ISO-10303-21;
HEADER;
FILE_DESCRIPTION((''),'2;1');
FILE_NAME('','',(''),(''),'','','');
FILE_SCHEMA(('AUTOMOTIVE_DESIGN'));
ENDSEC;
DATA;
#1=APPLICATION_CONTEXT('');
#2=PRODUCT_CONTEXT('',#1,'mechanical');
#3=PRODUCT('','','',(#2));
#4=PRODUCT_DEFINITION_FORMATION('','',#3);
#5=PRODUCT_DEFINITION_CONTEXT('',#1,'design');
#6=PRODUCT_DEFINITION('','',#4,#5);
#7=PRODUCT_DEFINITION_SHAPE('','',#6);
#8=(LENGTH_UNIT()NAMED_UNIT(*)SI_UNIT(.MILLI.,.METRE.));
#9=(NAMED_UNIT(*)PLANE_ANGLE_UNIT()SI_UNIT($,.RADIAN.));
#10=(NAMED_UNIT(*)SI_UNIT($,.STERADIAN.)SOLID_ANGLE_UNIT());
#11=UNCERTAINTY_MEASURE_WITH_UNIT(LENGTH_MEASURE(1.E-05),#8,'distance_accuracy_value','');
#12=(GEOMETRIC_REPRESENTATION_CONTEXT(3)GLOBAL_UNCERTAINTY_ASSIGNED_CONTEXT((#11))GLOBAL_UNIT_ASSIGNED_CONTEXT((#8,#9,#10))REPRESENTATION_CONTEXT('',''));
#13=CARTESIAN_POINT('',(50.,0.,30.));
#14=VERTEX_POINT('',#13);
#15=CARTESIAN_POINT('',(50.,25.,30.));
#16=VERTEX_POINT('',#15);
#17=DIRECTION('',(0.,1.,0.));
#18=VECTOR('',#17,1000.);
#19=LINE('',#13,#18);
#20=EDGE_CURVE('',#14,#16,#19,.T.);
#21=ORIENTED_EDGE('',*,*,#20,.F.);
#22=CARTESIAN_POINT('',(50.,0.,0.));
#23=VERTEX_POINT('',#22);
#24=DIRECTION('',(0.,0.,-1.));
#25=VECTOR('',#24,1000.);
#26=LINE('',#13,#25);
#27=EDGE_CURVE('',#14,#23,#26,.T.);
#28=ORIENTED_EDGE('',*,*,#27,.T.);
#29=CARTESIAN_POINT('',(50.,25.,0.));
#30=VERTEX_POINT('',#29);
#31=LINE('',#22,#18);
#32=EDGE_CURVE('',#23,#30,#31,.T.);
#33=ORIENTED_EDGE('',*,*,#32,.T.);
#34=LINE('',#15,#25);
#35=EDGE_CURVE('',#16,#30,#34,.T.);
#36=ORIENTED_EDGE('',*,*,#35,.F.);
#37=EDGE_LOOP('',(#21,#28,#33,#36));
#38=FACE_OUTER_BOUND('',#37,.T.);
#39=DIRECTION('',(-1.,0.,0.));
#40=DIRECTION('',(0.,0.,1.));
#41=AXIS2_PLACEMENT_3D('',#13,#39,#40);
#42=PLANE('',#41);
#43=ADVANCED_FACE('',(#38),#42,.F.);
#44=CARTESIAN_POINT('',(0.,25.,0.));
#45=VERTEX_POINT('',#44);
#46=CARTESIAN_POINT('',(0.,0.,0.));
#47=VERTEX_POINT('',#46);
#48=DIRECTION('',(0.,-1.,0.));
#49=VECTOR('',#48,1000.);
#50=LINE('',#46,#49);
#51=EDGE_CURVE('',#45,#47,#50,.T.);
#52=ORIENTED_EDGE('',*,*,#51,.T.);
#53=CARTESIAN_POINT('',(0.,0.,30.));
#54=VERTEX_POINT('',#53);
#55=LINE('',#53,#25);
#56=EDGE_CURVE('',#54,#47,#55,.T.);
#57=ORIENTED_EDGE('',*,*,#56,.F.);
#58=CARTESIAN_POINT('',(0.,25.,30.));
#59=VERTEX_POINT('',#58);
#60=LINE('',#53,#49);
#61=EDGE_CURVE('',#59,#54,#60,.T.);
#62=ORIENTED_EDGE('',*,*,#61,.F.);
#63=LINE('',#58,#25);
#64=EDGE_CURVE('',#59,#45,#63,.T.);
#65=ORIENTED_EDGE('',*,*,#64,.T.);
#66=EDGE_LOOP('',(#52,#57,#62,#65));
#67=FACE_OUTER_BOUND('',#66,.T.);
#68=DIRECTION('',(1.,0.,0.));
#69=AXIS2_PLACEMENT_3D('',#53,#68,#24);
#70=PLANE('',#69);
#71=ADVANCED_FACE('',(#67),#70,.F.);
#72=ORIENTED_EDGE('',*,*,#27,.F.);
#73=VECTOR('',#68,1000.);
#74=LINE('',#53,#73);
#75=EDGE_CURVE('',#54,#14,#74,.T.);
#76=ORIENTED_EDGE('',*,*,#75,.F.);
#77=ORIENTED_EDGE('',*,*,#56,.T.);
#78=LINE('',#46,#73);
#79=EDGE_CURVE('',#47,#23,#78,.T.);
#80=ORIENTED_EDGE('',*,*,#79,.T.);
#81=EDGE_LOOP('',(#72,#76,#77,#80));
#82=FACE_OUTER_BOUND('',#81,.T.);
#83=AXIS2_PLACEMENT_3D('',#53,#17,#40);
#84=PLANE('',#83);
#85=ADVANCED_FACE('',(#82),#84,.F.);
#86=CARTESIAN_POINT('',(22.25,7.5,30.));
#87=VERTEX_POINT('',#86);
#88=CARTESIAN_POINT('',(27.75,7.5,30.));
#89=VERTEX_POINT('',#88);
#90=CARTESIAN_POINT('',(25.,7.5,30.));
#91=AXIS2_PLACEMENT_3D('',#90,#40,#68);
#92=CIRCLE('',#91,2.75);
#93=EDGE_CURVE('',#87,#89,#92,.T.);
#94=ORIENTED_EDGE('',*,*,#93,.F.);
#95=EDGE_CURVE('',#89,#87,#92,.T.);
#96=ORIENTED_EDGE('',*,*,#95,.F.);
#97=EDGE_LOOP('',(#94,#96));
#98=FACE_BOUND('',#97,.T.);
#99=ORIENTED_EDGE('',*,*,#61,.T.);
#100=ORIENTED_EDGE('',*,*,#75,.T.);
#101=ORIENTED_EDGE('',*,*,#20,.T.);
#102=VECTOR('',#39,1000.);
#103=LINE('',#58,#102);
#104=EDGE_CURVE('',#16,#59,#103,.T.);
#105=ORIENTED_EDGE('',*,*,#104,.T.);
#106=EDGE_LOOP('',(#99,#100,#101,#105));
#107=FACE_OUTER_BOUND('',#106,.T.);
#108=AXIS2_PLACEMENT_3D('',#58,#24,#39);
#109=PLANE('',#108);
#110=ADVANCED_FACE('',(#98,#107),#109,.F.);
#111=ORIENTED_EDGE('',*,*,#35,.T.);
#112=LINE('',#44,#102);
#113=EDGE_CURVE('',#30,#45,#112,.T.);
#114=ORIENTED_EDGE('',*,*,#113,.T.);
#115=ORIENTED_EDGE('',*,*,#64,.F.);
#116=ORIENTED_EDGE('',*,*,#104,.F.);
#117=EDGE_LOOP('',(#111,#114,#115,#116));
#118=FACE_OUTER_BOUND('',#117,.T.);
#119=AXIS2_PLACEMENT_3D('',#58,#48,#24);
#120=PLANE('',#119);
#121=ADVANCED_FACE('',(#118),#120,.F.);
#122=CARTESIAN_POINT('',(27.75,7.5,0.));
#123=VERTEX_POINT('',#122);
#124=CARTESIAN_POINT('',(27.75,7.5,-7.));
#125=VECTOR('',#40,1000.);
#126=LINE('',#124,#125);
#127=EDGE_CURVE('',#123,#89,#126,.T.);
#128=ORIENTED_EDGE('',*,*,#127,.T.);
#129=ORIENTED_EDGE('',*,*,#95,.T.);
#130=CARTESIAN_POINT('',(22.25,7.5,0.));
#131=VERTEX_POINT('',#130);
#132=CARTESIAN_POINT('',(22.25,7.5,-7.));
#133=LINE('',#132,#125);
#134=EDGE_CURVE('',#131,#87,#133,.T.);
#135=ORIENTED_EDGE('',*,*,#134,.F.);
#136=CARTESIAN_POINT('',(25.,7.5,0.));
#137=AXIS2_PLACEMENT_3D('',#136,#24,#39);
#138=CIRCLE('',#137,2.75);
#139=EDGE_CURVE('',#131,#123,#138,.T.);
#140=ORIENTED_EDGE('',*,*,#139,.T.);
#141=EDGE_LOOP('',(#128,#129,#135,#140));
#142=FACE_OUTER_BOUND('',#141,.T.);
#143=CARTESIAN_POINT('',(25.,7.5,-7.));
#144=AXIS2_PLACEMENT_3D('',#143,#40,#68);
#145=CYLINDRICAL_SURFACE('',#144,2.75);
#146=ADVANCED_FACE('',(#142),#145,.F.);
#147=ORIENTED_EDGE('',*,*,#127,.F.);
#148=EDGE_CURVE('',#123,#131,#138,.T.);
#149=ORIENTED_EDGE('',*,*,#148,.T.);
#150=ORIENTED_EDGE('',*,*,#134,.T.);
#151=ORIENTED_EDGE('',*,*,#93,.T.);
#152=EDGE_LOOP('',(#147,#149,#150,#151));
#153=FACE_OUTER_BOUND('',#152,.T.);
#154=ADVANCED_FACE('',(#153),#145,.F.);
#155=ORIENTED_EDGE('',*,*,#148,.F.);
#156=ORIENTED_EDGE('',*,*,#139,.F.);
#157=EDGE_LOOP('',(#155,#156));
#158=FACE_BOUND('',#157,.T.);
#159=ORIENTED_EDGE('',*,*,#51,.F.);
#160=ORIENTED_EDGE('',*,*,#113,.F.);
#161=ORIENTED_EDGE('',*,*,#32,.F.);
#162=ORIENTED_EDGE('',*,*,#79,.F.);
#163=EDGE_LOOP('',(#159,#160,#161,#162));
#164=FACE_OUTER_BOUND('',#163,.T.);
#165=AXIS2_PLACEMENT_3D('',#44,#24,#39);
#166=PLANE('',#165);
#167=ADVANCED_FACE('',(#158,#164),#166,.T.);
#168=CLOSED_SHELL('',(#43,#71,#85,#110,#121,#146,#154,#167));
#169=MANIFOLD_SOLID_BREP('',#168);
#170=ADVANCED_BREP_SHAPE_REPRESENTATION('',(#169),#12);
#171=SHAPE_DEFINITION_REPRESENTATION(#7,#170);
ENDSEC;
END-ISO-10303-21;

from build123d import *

# Parameters (mm, degrees)
SKETCH_1_W          = 50
SKETCH_1_H          = 25
EXTRUDE_1_DEPTH     = 30
SKETCH_2_R          = 2.75
CUT_EXTRUDE_1_DEPTH = 37


with BuildPart() as part:
    # 草图1 → 凸台-拉伸1 (new body)
    with BuildSketch(Plane.XY):
        with Locations((25, 12.5)):
            Rectangle(SKETCH_1_W, SKETCH_1_H)
    extrude(amount=EXTRUDE_1_DEPTH)

    # 草图2 → 切除-拉伸1 (cut)
    with BuildSketch(Plane.XY.offset(30)):
        with Locations((25, 7.5)):
            Circle(SKETCH_2_R)
    extrude(amount=-CUT_EXTRUDE_1_DEPTH, mode=Mode.SUBTRACT)


solid = part.part
